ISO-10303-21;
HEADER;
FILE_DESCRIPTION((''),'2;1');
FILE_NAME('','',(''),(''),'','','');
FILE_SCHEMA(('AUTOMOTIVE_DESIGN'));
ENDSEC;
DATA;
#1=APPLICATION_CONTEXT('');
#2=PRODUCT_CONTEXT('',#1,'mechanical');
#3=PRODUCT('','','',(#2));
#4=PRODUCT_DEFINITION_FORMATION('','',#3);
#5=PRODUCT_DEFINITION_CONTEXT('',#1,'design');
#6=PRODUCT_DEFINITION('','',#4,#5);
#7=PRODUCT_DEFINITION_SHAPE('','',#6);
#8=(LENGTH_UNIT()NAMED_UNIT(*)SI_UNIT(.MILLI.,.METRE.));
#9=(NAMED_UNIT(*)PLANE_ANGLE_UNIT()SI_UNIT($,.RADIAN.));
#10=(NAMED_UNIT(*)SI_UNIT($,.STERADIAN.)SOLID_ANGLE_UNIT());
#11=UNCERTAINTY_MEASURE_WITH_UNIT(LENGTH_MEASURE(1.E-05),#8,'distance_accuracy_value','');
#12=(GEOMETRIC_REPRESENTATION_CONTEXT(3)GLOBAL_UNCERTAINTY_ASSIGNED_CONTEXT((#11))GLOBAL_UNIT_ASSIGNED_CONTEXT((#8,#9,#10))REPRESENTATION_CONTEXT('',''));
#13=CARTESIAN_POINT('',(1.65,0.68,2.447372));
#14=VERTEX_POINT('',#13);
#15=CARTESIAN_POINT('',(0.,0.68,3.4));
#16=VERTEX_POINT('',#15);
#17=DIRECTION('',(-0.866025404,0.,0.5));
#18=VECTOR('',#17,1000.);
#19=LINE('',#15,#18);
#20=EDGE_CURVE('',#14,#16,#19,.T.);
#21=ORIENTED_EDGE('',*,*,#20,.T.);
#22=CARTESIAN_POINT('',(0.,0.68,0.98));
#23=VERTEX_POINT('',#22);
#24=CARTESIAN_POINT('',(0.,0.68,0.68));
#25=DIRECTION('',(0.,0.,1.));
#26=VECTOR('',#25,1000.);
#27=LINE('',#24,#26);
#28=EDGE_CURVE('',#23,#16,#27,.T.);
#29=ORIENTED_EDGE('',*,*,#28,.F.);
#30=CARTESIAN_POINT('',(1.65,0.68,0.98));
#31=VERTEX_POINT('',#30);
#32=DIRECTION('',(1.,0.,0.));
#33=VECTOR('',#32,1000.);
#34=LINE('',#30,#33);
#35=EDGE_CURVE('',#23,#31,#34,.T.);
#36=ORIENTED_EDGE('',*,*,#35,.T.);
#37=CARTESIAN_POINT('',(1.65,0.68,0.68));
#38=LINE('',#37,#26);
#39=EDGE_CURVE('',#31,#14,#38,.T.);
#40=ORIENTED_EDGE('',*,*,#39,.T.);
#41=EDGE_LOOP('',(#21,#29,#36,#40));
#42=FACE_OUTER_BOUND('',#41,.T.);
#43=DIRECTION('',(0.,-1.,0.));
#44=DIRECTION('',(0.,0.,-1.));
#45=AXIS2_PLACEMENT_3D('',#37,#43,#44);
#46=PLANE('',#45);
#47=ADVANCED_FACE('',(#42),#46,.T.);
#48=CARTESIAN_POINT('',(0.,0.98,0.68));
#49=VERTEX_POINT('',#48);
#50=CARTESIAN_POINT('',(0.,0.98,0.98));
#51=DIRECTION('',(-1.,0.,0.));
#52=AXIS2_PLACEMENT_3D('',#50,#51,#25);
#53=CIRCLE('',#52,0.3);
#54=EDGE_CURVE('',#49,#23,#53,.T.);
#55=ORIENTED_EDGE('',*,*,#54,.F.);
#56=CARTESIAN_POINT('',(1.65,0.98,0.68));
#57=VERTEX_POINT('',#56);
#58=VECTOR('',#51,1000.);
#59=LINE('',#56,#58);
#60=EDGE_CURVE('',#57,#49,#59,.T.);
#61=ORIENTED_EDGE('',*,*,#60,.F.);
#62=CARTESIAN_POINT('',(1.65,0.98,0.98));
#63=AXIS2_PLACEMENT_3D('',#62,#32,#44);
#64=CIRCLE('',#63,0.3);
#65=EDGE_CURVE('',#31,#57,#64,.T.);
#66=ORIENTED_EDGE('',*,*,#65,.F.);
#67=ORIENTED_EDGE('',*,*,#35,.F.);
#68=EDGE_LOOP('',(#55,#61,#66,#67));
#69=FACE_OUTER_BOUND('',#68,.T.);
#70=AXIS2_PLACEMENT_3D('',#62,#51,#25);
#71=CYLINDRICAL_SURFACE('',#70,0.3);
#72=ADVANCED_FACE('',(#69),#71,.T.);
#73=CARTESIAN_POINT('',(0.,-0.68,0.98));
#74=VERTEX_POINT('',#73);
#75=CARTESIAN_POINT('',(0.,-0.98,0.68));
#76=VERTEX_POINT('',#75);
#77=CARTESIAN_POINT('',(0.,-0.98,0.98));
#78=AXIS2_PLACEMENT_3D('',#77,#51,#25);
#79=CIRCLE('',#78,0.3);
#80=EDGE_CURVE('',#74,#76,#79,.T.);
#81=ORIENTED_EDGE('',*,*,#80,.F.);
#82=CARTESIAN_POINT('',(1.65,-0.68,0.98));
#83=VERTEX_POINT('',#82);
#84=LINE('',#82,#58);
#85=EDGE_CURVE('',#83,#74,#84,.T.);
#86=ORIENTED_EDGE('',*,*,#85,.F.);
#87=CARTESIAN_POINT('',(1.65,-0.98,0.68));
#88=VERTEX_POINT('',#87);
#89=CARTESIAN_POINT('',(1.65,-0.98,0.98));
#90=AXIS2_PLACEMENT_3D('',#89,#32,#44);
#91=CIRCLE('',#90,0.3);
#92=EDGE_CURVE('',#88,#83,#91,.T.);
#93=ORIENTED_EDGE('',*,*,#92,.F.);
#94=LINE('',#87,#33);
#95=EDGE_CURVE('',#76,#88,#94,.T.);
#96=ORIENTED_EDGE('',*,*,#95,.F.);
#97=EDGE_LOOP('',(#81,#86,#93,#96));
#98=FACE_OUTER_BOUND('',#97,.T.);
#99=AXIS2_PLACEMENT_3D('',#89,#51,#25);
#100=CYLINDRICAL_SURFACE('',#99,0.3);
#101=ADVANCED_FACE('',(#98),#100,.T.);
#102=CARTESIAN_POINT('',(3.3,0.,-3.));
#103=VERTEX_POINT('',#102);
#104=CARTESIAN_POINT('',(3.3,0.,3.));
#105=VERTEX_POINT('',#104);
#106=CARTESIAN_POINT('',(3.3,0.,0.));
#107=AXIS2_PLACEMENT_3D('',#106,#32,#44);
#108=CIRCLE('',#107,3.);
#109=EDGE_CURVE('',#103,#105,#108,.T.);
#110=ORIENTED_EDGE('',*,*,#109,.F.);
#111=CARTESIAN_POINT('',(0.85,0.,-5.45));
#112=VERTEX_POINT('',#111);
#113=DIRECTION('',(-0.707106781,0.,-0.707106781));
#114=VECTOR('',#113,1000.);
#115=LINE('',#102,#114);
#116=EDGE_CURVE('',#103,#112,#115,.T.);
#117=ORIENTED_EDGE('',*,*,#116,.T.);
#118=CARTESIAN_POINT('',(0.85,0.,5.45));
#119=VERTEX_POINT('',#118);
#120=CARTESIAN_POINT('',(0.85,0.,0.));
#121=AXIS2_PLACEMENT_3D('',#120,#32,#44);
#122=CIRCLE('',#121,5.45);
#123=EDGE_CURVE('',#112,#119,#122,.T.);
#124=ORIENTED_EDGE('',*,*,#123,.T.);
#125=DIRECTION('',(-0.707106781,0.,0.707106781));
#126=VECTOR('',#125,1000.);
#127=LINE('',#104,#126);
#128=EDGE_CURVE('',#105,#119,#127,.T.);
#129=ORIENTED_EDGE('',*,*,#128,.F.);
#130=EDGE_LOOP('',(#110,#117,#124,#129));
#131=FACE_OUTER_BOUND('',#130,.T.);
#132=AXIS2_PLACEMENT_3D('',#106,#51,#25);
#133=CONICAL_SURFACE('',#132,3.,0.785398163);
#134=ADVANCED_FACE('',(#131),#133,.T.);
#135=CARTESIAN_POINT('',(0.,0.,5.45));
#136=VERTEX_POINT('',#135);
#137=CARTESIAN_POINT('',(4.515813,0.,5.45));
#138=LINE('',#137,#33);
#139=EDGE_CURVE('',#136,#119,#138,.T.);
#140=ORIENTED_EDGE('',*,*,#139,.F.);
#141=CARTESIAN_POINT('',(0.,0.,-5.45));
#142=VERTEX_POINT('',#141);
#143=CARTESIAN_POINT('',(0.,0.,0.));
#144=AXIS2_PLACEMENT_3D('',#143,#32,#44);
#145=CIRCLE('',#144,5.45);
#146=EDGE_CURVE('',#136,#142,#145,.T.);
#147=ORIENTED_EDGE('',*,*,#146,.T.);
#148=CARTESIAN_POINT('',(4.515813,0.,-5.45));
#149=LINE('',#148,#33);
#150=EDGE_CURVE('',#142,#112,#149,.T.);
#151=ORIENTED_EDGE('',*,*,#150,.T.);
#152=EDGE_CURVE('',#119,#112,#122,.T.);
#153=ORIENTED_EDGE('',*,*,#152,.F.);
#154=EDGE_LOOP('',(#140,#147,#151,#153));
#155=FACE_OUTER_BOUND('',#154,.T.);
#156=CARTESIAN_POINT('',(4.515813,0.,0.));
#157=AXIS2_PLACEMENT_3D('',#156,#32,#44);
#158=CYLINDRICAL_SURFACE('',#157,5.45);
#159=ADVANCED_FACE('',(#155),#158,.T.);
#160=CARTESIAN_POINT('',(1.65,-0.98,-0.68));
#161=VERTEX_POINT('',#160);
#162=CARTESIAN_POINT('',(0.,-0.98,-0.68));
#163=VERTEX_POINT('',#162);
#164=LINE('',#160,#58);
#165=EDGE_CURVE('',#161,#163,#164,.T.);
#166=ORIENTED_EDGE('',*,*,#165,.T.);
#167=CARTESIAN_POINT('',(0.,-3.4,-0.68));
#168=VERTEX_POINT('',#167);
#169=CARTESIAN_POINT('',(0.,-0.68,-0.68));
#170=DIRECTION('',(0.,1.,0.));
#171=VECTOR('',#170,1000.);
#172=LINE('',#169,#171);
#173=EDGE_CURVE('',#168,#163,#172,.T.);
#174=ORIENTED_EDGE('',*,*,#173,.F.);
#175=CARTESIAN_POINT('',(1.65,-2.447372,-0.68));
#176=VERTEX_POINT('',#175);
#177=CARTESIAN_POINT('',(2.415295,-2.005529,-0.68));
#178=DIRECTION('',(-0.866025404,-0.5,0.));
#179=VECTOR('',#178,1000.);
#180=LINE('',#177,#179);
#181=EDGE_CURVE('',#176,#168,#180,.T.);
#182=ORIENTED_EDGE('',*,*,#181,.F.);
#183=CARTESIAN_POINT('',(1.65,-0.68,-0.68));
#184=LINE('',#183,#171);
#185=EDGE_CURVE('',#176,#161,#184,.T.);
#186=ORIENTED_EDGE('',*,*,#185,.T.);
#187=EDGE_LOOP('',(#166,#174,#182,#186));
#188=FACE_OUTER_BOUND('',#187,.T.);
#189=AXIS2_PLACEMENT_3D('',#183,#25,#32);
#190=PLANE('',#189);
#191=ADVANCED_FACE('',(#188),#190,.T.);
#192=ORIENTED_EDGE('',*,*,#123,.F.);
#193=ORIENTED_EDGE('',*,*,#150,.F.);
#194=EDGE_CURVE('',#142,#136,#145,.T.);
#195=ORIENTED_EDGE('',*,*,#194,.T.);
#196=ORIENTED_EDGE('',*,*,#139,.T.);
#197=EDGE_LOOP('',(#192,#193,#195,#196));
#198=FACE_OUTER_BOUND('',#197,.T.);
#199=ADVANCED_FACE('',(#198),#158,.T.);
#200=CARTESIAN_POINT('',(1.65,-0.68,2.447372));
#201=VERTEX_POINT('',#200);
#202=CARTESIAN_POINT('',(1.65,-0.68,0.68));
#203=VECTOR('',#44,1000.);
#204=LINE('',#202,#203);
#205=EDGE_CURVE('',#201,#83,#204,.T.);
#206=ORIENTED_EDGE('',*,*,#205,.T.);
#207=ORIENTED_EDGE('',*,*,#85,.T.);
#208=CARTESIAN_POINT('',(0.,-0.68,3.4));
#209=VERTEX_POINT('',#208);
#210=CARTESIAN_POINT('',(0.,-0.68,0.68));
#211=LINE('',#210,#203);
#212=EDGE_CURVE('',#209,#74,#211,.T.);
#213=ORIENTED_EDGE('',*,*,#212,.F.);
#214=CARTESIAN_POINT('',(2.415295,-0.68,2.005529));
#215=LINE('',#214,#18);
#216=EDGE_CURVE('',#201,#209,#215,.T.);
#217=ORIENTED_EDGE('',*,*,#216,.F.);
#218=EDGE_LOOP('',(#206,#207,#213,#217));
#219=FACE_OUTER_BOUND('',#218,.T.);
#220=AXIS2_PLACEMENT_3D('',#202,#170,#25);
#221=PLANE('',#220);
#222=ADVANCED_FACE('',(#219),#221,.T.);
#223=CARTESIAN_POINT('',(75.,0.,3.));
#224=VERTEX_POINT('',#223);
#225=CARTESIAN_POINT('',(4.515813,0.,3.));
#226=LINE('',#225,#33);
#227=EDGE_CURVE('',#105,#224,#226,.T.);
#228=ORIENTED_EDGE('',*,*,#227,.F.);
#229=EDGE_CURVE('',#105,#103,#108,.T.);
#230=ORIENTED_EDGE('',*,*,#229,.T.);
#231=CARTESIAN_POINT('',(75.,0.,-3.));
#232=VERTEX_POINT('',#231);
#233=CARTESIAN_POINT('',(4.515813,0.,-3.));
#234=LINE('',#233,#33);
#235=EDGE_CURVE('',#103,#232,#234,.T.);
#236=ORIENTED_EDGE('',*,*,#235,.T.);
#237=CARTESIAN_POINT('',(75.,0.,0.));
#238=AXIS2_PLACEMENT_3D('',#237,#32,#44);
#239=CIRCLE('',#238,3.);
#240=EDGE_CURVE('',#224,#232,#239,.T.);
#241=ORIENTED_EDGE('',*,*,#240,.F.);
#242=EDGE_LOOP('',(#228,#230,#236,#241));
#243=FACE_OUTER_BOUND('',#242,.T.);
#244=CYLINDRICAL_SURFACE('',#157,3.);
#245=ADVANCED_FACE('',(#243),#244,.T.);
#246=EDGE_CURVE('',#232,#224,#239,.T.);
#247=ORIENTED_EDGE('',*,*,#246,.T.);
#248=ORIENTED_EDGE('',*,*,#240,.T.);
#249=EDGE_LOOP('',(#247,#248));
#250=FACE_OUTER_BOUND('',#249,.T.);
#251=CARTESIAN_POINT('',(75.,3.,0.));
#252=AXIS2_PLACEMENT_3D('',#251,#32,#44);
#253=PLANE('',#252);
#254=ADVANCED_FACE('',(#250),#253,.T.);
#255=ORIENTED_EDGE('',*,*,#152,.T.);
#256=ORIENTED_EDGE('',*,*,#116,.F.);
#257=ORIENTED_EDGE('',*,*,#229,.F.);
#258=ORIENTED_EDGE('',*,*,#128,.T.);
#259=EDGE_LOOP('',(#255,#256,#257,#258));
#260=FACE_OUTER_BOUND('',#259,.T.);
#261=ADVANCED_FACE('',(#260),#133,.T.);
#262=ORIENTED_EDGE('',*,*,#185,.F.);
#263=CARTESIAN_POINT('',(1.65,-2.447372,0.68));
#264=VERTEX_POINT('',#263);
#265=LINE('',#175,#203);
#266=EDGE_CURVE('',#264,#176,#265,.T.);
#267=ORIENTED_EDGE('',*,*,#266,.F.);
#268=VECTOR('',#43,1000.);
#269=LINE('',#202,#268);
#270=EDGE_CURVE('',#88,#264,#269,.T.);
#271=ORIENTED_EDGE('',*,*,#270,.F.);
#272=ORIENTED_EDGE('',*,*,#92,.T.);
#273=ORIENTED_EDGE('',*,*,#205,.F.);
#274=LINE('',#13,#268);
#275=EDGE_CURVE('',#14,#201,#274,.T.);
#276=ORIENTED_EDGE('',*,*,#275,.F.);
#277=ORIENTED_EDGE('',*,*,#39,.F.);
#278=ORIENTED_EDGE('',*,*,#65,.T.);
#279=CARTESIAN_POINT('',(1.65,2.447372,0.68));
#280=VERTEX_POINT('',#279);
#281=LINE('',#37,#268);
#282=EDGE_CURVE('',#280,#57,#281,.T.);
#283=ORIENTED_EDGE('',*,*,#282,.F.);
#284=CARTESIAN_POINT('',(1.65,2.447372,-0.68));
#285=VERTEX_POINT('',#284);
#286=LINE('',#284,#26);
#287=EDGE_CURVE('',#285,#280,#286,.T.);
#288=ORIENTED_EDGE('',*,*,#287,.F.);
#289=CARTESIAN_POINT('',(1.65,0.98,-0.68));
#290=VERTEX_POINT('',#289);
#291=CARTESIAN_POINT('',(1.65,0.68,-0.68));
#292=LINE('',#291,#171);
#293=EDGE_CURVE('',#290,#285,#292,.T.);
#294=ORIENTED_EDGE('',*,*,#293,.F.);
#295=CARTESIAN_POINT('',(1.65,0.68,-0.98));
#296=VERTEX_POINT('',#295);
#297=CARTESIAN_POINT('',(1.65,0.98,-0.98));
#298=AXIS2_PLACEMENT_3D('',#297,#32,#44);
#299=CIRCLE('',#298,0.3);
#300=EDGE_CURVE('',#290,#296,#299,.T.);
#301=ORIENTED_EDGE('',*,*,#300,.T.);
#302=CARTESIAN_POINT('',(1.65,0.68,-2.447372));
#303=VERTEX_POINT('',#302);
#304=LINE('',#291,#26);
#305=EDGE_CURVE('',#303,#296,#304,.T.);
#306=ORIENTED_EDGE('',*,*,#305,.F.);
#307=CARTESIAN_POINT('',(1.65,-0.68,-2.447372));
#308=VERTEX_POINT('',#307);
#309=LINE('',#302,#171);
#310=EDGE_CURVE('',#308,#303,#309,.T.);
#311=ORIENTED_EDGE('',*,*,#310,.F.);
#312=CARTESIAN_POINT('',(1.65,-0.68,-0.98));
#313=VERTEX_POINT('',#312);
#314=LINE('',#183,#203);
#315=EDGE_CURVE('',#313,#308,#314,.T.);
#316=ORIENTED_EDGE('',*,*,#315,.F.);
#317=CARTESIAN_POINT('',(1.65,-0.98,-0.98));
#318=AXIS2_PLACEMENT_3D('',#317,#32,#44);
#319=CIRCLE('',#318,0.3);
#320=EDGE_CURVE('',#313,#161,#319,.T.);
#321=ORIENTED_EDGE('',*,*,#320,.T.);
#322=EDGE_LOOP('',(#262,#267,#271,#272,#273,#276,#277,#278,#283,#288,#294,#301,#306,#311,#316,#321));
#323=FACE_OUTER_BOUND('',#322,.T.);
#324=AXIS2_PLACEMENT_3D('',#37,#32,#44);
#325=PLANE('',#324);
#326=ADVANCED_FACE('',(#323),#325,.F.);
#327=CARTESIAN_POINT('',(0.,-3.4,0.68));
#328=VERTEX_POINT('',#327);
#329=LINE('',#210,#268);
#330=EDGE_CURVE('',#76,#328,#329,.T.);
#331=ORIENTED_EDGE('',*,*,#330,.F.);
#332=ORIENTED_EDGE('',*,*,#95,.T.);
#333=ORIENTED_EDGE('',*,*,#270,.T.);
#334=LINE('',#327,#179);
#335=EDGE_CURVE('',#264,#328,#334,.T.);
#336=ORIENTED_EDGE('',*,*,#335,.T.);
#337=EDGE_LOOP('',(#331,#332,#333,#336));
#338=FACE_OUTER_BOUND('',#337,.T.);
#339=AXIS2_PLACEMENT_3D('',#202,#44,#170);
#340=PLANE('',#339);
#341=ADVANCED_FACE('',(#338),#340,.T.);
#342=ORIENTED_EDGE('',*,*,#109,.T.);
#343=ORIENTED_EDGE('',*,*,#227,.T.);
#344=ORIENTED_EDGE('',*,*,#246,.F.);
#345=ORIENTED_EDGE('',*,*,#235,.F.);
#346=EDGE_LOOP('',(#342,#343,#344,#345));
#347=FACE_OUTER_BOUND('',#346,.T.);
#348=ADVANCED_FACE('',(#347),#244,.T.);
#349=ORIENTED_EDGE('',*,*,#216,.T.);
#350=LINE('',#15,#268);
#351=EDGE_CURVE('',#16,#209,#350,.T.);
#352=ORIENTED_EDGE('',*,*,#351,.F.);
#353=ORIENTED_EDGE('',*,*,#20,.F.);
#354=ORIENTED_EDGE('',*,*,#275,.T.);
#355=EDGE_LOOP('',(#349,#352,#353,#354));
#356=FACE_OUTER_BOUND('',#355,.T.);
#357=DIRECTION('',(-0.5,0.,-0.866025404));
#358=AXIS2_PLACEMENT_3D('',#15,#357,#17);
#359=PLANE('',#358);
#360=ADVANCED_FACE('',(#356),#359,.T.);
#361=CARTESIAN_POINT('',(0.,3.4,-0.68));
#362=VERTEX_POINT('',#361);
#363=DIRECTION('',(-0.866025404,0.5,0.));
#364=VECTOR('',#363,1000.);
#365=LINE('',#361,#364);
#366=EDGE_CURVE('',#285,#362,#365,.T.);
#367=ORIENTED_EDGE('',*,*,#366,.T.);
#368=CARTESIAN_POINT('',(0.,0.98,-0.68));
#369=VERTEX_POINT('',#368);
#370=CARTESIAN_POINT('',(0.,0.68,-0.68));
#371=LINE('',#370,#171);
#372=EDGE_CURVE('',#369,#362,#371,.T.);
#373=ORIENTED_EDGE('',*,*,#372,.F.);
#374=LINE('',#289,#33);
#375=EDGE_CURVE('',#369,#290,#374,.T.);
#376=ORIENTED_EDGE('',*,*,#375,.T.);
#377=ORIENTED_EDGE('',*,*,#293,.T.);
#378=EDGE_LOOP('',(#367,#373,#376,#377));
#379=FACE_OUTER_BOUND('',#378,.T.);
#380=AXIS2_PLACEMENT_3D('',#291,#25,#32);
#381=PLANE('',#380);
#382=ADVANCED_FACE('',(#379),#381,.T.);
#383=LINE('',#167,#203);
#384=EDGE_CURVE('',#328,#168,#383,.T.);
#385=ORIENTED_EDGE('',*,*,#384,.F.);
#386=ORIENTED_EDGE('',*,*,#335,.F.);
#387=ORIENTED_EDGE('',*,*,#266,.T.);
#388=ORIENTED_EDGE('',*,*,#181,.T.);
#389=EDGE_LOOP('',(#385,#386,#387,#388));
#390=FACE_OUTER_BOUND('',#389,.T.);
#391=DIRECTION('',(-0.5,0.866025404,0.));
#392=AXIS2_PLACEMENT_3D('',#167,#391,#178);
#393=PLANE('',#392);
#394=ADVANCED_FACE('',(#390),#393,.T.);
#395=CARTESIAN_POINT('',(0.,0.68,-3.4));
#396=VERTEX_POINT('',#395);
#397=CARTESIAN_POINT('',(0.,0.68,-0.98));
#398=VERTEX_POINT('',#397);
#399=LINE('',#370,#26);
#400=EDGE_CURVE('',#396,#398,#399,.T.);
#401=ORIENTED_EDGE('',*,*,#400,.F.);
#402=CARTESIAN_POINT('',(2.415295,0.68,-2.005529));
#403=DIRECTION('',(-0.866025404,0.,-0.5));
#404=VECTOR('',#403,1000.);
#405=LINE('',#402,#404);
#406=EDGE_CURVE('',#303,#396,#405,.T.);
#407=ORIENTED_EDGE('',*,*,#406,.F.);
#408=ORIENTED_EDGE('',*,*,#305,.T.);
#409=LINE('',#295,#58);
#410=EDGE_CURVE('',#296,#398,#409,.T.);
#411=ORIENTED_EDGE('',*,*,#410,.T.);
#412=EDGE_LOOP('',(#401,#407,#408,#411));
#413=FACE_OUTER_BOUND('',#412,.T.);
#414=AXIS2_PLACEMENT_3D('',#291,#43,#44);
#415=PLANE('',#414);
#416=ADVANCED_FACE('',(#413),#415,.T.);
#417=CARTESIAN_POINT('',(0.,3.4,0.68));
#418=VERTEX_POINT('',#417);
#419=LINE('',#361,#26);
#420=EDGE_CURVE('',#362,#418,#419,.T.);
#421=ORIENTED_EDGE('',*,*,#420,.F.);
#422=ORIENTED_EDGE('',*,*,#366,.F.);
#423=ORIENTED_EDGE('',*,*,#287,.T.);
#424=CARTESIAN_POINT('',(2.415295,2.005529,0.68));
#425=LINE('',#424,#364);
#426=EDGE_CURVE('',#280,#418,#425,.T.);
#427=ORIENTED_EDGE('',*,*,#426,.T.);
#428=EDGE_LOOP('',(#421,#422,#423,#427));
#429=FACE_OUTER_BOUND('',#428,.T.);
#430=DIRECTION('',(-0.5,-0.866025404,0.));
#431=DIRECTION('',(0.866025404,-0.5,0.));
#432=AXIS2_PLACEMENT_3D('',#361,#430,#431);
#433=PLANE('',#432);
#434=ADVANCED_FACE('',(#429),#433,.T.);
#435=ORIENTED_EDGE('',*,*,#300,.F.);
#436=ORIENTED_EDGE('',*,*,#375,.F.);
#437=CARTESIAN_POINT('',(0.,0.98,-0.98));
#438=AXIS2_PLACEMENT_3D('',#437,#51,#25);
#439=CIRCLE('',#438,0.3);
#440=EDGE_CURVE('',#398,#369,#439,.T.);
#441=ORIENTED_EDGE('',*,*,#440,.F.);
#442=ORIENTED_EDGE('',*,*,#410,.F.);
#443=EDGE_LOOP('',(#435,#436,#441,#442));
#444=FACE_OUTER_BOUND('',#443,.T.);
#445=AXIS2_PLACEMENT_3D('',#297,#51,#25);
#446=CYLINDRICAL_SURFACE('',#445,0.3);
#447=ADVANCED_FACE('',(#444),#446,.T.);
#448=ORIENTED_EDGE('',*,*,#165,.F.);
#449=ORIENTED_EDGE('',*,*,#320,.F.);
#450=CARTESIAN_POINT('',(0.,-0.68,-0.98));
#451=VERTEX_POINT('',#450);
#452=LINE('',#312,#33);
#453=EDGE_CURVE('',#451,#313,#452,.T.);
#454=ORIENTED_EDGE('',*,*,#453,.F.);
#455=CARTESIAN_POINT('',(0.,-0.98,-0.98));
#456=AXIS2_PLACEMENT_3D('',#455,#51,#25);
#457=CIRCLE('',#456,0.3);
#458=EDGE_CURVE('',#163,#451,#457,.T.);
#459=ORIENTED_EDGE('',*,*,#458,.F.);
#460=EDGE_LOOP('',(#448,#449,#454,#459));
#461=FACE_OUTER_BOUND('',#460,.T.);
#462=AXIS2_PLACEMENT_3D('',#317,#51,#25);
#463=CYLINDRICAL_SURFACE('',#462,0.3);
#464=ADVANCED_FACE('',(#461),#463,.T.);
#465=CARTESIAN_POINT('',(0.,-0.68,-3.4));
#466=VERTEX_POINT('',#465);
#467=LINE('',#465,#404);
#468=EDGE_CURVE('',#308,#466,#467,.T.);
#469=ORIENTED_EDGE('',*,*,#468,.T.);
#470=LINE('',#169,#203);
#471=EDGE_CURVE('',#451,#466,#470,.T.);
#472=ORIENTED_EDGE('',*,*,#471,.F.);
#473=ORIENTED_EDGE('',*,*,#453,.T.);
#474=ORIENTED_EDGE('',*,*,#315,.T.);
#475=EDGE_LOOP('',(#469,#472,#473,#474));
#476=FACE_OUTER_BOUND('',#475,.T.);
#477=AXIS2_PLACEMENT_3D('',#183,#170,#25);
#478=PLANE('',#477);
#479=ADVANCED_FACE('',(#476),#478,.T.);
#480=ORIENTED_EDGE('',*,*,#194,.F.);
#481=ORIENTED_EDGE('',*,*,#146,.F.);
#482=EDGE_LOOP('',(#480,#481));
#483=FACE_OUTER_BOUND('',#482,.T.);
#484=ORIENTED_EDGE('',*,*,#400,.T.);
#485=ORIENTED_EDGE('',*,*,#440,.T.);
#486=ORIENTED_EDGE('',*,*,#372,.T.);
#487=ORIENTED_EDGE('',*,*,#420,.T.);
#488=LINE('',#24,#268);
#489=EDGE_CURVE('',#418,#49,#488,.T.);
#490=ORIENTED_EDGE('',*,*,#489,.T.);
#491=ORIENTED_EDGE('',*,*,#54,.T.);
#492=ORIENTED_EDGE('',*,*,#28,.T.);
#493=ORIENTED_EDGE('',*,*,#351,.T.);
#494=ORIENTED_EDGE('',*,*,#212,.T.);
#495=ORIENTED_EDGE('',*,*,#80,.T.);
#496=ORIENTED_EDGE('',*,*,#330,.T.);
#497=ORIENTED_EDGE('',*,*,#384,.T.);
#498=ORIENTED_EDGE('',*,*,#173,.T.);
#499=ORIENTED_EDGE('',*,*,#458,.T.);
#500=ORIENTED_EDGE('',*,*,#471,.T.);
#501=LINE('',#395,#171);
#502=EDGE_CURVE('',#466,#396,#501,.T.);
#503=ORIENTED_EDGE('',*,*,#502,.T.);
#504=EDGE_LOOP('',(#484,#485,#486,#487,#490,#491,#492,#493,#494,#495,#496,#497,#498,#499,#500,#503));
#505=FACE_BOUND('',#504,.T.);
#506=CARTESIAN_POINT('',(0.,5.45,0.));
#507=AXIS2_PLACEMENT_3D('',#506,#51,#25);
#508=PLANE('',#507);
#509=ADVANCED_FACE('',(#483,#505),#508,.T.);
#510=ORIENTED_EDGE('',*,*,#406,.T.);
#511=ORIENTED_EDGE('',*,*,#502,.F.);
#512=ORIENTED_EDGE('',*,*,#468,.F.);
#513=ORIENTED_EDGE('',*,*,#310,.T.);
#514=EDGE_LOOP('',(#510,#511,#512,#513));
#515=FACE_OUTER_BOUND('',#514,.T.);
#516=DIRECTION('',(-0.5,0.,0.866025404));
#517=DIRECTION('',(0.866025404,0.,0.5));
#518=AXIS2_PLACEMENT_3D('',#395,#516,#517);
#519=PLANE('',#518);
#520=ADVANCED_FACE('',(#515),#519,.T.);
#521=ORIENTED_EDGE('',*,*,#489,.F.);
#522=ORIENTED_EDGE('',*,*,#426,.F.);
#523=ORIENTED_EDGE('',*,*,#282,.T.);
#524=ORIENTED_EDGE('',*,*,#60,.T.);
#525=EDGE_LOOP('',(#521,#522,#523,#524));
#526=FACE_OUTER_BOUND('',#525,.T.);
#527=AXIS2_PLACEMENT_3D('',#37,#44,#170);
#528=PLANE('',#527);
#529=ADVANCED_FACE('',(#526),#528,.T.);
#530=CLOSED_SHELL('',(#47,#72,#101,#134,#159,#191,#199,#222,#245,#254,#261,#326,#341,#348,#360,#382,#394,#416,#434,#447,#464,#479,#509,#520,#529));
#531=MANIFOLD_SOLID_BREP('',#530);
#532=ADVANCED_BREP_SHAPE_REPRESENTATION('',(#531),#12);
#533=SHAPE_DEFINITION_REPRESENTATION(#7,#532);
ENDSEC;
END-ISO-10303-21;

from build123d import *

# Parameters (mm, degrees)
CROSSRECESS_DEPTH = 1.65
DRAFT9_ANGLE      = 30
FILLET5_R         = 0.3
SKETCH10_W        = 1
SKETCH10_H        = 3


with BuildPart() as part:
    # Sketch1 → Base (revolve)
    with BuildSketch(Plane.XY, mode=Mode.PRIVATE) as base_sk:
        Polygon((75, 3), (5.3, 3), (3.3, 3), (0.85, 5.45), (0, 5.45), (0, 0), (75, 0), align=None)
    revolve(base_sk.sketch.rotate(Axis((4.515812911, 0, 0), (-1, 0, 0)), 90), axis=Axis((4.515812911, 0, 0), (-1, 0, 0)))

    # Sketch6 → CrossRecess (cut)
    with BuildSketch(Plane(origin=(0, 0, 0), x_dir=(0, 0, -1), z_dir=(1, 0, 0))):
        Polygon((0.68, 0.68), (0.68, 3.4), (-0.68, 3.4), (-0.68, 0.68), (-3.4, 0.68), (-3.4, -0.68), (-0.68, -0.68), (-0.68, -3.4), (0.68, -3.4), (0.68, -0.68), (3.4, -0.68), (3.4, 0.68), align=None)
    extrude(amount=CROSSRECESS_DEPTH, mode=Mode.SUBTRACT)

    # Draft9
    draft9_faces = [part.faces().sort_by_distance(p)[0] for p in [
        (0.825, -3.4, 0),
        (0.825, 0, 3.4),
        (0.825, 0, -3.4),
        (0.825, 3.4, 0),
    ]]
    draft(draft9_faces, Plane(origin=(0, 5.45, 0), x_dir=(0, 0, -1), z_dir=(-1, 0, 0)), DRAFT9_ANGLE)

    # Fillet5
    fillet5_edges = [part.edges().sort_by_distance(p)[0] for p in [
        (0.825, 0.68, 0.68),
        (0.825, -0.68, 0.68),
        (0.825, -0.68, -0.68),
        (0.825, 0.68, -0.68),
    ]]
    fillet(fillet5_edges, radius=FILLET5_R)

    # Sketch10 → Revolve2 (revolve)
    with BuildSketch(Plane.XY):
        with Locations((3.8, 1.5)):
            Rectangle(SKETCH10_W, SKETCH10_H)
    revolve(axis=Axis((62.228915663, 0, 0), (-1, 0, 0)))


solid = part.part
